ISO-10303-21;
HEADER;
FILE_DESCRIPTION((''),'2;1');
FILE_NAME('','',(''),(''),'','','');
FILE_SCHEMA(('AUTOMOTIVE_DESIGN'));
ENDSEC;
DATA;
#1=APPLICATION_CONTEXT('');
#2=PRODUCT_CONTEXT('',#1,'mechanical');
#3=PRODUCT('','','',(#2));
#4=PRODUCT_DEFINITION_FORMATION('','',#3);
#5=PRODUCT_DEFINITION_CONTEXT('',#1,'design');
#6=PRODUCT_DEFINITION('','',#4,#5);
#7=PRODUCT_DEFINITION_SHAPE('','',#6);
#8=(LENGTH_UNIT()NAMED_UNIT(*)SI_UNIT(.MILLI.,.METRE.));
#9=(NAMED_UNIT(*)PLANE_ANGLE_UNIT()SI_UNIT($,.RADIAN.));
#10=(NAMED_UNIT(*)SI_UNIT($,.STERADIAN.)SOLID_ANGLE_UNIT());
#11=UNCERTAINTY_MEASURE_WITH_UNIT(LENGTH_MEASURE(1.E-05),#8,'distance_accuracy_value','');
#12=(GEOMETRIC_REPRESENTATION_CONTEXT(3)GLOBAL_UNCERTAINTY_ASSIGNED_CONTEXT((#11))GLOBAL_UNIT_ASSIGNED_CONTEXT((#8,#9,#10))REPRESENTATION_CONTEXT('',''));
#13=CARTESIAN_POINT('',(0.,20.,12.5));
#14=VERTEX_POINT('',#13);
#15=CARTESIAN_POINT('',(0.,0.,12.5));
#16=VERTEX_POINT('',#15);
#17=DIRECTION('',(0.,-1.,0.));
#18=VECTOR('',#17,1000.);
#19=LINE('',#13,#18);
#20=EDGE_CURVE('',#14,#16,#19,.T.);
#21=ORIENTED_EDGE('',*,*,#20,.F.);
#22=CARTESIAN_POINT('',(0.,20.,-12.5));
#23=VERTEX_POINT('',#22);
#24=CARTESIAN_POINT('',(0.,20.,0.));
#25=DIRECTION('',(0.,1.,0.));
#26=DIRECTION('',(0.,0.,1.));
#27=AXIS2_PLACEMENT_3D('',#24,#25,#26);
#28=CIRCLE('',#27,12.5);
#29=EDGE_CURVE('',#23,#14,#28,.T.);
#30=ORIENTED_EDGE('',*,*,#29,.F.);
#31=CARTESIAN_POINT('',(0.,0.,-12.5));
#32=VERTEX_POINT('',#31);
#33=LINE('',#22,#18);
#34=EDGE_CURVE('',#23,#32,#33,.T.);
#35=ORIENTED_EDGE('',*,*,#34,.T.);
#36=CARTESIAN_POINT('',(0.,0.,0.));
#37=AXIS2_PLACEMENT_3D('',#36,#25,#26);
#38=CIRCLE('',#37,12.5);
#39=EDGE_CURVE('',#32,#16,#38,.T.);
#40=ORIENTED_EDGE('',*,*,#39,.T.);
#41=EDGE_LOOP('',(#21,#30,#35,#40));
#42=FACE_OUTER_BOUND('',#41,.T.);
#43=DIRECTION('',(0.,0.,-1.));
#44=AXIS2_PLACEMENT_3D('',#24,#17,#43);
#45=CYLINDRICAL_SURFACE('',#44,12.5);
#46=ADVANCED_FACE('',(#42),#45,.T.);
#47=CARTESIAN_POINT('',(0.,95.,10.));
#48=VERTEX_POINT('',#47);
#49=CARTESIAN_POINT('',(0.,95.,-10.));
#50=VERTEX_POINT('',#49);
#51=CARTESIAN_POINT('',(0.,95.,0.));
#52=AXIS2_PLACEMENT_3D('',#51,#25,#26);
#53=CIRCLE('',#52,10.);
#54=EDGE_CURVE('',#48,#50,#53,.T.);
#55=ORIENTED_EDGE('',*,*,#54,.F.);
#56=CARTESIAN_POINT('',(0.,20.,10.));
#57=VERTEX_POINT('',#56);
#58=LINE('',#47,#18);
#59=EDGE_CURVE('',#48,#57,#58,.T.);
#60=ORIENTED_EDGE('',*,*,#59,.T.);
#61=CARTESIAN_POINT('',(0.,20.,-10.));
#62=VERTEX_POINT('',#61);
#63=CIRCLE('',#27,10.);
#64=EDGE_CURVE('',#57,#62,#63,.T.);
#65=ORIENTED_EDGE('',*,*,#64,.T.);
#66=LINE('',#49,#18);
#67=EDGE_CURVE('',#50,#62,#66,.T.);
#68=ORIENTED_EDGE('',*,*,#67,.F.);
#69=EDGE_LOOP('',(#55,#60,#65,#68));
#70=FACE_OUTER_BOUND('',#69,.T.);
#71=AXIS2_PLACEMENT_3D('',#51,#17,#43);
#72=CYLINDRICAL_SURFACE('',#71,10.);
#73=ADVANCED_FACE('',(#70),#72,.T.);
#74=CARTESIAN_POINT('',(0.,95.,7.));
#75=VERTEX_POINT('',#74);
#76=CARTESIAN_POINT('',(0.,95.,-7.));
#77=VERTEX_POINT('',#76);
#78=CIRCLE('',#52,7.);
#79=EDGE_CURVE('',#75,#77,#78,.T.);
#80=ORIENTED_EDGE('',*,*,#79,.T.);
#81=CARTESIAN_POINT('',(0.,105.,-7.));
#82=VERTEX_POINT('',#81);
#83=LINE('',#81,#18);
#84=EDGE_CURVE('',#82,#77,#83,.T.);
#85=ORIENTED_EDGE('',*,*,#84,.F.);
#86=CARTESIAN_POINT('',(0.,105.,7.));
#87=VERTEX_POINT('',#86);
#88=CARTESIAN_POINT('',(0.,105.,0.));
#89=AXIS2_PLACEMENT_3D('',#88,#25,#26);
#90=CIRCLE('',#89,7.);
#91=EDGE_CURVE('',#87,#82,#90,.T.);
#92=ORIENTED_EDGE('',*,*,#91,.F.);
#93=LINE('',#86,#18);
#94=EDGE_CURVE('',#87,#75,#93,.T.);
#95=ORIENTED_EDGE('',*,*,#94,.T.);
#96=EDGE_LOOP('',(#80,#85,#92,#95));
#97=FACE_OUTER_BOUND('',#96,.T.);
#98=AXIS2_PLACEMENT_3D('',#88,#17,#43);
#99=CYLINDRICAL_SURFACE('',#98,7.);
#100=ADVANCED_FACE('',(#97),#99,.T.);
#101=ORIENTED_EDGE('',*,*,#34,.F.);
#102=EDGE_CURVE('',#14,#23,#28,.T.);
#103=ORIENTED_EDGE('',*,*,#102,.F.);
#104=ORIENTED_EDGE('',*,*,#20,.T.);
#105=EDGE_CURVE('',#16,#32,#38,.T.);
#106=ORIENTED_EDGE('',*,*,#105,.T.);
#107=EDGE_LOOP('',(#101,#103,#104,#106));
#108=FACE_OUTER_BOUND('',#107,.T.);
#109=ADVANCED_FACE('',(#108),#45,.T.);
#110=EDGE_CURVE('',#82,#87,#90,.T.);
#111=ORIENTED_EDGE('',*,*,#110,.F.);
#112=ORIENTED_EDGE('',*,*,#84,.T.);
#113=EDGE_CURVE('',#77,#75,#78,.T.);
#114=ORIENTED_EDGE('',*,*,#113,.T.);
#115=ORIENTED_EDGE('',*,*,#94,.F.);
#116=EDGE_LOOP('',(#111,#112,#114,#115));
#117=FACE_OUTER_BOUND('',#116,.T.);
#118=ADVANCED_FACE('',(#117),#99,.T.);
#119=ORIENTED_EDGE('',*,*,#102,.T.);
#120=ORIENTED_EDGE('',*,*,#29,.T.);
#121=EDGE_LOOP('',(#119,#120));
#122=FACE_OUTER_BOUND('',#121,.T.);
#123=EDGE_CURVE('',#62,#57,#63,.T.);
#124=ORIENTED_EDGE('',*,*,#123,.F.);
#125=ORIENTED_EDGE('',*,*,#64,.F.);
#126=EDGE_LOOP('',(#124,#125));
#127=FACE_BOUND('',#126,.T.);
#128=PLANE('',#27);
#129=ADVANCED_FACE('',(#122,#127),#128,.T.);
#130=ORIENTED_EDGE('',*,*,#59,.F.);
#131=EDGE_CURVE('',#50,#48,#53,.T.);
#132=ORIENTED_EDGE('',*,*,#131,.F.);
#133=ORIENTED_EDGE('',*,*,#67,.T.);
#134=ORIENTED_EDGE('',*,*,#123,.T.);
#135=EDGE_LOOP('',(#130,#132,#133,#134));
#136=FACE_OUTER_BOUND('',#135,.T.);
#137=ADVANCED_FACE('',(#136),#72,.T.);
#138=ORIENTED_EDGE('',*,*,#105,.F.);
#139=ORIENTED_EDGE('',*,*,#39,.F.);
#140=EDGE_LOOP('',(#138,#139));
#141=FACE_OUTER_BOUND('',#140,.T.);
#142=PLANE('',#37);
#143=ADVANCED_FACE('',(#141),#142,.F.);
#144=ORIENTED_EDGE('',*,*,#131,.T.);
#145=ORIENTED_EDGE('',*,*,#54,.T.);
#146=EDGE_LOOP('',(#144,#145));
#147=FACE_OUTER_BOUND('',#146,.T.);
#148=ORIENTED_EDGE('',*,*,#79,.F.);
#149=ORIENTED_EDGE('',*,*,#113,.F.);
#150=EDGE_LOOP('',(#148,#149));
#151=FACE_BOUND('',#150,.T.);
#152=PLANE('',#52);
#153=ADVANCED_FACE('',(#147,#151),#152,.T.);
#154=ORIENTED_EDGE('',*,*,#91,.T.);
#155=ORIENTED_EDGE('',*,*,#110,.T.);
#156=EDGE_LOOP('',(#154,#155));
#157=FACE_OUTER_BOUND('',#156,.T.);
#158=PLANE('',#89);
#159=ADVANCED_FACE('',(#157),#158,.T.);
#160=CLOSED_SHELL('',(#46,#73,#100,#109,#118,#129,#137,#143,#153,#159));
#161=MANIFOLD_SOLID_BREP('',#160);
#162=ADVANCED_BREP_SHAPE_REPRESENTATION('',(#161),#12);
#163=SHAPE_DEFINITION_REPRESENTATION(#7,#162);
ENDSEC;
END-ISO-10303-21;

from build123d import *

# Parameters (mm, degrees)
SKETCH1_R           = 12.5
BOSS_EXTRUDE1_DEPTH = 20
SKETCH2_R           = 10
BOSS_EXTRUDE2_DEPTH = 75
SKETCH3_R           = 7
BOSS_EXTRUDE3_DEPTH = 10


with BuildPart() as part:
    # Sketch1 → Boss-Extrude1 (new body)
    with BuildSketch(Plane(origin=(0, 0, 0), x_dir=(1, 0, 0), z_dir=(0, 1, 0))):
        with Locations(Location((0, 0, 0), (0, 0, 270))):
            Circle(SKETCH1_R)
    extrude(amount=BOSS_EXTRUDE1_DEPTH)

    # Sketch2 → Boss-Extrude2 (add)
    with BuildSketch(Plane(origin=(0, 20, 0), x_dir=(1, 0, 0), z_dir=(0, 1, 0))):
        with Locations(Location((0, 0, 0), (0, 0, 270))):
            Circle(SKETCH2_R)
    extrude(amount=BOSS_EXTRUDE2_DEPTH)

    # Sketch3 → Boss-Extrude3 (add)
    with BuildSketch(Plane(origin=(0, 95, 0), x_dir=(1, 0, 0), z_dir=(0, 1, 0))):
        with Locations(Location((0, 0, 0), (0, 0, 270))):
            Circle(SKETCH3_R)
    extrude(amount=BOSS_EXTRUDE3_DEPTH)


solid = part.part
